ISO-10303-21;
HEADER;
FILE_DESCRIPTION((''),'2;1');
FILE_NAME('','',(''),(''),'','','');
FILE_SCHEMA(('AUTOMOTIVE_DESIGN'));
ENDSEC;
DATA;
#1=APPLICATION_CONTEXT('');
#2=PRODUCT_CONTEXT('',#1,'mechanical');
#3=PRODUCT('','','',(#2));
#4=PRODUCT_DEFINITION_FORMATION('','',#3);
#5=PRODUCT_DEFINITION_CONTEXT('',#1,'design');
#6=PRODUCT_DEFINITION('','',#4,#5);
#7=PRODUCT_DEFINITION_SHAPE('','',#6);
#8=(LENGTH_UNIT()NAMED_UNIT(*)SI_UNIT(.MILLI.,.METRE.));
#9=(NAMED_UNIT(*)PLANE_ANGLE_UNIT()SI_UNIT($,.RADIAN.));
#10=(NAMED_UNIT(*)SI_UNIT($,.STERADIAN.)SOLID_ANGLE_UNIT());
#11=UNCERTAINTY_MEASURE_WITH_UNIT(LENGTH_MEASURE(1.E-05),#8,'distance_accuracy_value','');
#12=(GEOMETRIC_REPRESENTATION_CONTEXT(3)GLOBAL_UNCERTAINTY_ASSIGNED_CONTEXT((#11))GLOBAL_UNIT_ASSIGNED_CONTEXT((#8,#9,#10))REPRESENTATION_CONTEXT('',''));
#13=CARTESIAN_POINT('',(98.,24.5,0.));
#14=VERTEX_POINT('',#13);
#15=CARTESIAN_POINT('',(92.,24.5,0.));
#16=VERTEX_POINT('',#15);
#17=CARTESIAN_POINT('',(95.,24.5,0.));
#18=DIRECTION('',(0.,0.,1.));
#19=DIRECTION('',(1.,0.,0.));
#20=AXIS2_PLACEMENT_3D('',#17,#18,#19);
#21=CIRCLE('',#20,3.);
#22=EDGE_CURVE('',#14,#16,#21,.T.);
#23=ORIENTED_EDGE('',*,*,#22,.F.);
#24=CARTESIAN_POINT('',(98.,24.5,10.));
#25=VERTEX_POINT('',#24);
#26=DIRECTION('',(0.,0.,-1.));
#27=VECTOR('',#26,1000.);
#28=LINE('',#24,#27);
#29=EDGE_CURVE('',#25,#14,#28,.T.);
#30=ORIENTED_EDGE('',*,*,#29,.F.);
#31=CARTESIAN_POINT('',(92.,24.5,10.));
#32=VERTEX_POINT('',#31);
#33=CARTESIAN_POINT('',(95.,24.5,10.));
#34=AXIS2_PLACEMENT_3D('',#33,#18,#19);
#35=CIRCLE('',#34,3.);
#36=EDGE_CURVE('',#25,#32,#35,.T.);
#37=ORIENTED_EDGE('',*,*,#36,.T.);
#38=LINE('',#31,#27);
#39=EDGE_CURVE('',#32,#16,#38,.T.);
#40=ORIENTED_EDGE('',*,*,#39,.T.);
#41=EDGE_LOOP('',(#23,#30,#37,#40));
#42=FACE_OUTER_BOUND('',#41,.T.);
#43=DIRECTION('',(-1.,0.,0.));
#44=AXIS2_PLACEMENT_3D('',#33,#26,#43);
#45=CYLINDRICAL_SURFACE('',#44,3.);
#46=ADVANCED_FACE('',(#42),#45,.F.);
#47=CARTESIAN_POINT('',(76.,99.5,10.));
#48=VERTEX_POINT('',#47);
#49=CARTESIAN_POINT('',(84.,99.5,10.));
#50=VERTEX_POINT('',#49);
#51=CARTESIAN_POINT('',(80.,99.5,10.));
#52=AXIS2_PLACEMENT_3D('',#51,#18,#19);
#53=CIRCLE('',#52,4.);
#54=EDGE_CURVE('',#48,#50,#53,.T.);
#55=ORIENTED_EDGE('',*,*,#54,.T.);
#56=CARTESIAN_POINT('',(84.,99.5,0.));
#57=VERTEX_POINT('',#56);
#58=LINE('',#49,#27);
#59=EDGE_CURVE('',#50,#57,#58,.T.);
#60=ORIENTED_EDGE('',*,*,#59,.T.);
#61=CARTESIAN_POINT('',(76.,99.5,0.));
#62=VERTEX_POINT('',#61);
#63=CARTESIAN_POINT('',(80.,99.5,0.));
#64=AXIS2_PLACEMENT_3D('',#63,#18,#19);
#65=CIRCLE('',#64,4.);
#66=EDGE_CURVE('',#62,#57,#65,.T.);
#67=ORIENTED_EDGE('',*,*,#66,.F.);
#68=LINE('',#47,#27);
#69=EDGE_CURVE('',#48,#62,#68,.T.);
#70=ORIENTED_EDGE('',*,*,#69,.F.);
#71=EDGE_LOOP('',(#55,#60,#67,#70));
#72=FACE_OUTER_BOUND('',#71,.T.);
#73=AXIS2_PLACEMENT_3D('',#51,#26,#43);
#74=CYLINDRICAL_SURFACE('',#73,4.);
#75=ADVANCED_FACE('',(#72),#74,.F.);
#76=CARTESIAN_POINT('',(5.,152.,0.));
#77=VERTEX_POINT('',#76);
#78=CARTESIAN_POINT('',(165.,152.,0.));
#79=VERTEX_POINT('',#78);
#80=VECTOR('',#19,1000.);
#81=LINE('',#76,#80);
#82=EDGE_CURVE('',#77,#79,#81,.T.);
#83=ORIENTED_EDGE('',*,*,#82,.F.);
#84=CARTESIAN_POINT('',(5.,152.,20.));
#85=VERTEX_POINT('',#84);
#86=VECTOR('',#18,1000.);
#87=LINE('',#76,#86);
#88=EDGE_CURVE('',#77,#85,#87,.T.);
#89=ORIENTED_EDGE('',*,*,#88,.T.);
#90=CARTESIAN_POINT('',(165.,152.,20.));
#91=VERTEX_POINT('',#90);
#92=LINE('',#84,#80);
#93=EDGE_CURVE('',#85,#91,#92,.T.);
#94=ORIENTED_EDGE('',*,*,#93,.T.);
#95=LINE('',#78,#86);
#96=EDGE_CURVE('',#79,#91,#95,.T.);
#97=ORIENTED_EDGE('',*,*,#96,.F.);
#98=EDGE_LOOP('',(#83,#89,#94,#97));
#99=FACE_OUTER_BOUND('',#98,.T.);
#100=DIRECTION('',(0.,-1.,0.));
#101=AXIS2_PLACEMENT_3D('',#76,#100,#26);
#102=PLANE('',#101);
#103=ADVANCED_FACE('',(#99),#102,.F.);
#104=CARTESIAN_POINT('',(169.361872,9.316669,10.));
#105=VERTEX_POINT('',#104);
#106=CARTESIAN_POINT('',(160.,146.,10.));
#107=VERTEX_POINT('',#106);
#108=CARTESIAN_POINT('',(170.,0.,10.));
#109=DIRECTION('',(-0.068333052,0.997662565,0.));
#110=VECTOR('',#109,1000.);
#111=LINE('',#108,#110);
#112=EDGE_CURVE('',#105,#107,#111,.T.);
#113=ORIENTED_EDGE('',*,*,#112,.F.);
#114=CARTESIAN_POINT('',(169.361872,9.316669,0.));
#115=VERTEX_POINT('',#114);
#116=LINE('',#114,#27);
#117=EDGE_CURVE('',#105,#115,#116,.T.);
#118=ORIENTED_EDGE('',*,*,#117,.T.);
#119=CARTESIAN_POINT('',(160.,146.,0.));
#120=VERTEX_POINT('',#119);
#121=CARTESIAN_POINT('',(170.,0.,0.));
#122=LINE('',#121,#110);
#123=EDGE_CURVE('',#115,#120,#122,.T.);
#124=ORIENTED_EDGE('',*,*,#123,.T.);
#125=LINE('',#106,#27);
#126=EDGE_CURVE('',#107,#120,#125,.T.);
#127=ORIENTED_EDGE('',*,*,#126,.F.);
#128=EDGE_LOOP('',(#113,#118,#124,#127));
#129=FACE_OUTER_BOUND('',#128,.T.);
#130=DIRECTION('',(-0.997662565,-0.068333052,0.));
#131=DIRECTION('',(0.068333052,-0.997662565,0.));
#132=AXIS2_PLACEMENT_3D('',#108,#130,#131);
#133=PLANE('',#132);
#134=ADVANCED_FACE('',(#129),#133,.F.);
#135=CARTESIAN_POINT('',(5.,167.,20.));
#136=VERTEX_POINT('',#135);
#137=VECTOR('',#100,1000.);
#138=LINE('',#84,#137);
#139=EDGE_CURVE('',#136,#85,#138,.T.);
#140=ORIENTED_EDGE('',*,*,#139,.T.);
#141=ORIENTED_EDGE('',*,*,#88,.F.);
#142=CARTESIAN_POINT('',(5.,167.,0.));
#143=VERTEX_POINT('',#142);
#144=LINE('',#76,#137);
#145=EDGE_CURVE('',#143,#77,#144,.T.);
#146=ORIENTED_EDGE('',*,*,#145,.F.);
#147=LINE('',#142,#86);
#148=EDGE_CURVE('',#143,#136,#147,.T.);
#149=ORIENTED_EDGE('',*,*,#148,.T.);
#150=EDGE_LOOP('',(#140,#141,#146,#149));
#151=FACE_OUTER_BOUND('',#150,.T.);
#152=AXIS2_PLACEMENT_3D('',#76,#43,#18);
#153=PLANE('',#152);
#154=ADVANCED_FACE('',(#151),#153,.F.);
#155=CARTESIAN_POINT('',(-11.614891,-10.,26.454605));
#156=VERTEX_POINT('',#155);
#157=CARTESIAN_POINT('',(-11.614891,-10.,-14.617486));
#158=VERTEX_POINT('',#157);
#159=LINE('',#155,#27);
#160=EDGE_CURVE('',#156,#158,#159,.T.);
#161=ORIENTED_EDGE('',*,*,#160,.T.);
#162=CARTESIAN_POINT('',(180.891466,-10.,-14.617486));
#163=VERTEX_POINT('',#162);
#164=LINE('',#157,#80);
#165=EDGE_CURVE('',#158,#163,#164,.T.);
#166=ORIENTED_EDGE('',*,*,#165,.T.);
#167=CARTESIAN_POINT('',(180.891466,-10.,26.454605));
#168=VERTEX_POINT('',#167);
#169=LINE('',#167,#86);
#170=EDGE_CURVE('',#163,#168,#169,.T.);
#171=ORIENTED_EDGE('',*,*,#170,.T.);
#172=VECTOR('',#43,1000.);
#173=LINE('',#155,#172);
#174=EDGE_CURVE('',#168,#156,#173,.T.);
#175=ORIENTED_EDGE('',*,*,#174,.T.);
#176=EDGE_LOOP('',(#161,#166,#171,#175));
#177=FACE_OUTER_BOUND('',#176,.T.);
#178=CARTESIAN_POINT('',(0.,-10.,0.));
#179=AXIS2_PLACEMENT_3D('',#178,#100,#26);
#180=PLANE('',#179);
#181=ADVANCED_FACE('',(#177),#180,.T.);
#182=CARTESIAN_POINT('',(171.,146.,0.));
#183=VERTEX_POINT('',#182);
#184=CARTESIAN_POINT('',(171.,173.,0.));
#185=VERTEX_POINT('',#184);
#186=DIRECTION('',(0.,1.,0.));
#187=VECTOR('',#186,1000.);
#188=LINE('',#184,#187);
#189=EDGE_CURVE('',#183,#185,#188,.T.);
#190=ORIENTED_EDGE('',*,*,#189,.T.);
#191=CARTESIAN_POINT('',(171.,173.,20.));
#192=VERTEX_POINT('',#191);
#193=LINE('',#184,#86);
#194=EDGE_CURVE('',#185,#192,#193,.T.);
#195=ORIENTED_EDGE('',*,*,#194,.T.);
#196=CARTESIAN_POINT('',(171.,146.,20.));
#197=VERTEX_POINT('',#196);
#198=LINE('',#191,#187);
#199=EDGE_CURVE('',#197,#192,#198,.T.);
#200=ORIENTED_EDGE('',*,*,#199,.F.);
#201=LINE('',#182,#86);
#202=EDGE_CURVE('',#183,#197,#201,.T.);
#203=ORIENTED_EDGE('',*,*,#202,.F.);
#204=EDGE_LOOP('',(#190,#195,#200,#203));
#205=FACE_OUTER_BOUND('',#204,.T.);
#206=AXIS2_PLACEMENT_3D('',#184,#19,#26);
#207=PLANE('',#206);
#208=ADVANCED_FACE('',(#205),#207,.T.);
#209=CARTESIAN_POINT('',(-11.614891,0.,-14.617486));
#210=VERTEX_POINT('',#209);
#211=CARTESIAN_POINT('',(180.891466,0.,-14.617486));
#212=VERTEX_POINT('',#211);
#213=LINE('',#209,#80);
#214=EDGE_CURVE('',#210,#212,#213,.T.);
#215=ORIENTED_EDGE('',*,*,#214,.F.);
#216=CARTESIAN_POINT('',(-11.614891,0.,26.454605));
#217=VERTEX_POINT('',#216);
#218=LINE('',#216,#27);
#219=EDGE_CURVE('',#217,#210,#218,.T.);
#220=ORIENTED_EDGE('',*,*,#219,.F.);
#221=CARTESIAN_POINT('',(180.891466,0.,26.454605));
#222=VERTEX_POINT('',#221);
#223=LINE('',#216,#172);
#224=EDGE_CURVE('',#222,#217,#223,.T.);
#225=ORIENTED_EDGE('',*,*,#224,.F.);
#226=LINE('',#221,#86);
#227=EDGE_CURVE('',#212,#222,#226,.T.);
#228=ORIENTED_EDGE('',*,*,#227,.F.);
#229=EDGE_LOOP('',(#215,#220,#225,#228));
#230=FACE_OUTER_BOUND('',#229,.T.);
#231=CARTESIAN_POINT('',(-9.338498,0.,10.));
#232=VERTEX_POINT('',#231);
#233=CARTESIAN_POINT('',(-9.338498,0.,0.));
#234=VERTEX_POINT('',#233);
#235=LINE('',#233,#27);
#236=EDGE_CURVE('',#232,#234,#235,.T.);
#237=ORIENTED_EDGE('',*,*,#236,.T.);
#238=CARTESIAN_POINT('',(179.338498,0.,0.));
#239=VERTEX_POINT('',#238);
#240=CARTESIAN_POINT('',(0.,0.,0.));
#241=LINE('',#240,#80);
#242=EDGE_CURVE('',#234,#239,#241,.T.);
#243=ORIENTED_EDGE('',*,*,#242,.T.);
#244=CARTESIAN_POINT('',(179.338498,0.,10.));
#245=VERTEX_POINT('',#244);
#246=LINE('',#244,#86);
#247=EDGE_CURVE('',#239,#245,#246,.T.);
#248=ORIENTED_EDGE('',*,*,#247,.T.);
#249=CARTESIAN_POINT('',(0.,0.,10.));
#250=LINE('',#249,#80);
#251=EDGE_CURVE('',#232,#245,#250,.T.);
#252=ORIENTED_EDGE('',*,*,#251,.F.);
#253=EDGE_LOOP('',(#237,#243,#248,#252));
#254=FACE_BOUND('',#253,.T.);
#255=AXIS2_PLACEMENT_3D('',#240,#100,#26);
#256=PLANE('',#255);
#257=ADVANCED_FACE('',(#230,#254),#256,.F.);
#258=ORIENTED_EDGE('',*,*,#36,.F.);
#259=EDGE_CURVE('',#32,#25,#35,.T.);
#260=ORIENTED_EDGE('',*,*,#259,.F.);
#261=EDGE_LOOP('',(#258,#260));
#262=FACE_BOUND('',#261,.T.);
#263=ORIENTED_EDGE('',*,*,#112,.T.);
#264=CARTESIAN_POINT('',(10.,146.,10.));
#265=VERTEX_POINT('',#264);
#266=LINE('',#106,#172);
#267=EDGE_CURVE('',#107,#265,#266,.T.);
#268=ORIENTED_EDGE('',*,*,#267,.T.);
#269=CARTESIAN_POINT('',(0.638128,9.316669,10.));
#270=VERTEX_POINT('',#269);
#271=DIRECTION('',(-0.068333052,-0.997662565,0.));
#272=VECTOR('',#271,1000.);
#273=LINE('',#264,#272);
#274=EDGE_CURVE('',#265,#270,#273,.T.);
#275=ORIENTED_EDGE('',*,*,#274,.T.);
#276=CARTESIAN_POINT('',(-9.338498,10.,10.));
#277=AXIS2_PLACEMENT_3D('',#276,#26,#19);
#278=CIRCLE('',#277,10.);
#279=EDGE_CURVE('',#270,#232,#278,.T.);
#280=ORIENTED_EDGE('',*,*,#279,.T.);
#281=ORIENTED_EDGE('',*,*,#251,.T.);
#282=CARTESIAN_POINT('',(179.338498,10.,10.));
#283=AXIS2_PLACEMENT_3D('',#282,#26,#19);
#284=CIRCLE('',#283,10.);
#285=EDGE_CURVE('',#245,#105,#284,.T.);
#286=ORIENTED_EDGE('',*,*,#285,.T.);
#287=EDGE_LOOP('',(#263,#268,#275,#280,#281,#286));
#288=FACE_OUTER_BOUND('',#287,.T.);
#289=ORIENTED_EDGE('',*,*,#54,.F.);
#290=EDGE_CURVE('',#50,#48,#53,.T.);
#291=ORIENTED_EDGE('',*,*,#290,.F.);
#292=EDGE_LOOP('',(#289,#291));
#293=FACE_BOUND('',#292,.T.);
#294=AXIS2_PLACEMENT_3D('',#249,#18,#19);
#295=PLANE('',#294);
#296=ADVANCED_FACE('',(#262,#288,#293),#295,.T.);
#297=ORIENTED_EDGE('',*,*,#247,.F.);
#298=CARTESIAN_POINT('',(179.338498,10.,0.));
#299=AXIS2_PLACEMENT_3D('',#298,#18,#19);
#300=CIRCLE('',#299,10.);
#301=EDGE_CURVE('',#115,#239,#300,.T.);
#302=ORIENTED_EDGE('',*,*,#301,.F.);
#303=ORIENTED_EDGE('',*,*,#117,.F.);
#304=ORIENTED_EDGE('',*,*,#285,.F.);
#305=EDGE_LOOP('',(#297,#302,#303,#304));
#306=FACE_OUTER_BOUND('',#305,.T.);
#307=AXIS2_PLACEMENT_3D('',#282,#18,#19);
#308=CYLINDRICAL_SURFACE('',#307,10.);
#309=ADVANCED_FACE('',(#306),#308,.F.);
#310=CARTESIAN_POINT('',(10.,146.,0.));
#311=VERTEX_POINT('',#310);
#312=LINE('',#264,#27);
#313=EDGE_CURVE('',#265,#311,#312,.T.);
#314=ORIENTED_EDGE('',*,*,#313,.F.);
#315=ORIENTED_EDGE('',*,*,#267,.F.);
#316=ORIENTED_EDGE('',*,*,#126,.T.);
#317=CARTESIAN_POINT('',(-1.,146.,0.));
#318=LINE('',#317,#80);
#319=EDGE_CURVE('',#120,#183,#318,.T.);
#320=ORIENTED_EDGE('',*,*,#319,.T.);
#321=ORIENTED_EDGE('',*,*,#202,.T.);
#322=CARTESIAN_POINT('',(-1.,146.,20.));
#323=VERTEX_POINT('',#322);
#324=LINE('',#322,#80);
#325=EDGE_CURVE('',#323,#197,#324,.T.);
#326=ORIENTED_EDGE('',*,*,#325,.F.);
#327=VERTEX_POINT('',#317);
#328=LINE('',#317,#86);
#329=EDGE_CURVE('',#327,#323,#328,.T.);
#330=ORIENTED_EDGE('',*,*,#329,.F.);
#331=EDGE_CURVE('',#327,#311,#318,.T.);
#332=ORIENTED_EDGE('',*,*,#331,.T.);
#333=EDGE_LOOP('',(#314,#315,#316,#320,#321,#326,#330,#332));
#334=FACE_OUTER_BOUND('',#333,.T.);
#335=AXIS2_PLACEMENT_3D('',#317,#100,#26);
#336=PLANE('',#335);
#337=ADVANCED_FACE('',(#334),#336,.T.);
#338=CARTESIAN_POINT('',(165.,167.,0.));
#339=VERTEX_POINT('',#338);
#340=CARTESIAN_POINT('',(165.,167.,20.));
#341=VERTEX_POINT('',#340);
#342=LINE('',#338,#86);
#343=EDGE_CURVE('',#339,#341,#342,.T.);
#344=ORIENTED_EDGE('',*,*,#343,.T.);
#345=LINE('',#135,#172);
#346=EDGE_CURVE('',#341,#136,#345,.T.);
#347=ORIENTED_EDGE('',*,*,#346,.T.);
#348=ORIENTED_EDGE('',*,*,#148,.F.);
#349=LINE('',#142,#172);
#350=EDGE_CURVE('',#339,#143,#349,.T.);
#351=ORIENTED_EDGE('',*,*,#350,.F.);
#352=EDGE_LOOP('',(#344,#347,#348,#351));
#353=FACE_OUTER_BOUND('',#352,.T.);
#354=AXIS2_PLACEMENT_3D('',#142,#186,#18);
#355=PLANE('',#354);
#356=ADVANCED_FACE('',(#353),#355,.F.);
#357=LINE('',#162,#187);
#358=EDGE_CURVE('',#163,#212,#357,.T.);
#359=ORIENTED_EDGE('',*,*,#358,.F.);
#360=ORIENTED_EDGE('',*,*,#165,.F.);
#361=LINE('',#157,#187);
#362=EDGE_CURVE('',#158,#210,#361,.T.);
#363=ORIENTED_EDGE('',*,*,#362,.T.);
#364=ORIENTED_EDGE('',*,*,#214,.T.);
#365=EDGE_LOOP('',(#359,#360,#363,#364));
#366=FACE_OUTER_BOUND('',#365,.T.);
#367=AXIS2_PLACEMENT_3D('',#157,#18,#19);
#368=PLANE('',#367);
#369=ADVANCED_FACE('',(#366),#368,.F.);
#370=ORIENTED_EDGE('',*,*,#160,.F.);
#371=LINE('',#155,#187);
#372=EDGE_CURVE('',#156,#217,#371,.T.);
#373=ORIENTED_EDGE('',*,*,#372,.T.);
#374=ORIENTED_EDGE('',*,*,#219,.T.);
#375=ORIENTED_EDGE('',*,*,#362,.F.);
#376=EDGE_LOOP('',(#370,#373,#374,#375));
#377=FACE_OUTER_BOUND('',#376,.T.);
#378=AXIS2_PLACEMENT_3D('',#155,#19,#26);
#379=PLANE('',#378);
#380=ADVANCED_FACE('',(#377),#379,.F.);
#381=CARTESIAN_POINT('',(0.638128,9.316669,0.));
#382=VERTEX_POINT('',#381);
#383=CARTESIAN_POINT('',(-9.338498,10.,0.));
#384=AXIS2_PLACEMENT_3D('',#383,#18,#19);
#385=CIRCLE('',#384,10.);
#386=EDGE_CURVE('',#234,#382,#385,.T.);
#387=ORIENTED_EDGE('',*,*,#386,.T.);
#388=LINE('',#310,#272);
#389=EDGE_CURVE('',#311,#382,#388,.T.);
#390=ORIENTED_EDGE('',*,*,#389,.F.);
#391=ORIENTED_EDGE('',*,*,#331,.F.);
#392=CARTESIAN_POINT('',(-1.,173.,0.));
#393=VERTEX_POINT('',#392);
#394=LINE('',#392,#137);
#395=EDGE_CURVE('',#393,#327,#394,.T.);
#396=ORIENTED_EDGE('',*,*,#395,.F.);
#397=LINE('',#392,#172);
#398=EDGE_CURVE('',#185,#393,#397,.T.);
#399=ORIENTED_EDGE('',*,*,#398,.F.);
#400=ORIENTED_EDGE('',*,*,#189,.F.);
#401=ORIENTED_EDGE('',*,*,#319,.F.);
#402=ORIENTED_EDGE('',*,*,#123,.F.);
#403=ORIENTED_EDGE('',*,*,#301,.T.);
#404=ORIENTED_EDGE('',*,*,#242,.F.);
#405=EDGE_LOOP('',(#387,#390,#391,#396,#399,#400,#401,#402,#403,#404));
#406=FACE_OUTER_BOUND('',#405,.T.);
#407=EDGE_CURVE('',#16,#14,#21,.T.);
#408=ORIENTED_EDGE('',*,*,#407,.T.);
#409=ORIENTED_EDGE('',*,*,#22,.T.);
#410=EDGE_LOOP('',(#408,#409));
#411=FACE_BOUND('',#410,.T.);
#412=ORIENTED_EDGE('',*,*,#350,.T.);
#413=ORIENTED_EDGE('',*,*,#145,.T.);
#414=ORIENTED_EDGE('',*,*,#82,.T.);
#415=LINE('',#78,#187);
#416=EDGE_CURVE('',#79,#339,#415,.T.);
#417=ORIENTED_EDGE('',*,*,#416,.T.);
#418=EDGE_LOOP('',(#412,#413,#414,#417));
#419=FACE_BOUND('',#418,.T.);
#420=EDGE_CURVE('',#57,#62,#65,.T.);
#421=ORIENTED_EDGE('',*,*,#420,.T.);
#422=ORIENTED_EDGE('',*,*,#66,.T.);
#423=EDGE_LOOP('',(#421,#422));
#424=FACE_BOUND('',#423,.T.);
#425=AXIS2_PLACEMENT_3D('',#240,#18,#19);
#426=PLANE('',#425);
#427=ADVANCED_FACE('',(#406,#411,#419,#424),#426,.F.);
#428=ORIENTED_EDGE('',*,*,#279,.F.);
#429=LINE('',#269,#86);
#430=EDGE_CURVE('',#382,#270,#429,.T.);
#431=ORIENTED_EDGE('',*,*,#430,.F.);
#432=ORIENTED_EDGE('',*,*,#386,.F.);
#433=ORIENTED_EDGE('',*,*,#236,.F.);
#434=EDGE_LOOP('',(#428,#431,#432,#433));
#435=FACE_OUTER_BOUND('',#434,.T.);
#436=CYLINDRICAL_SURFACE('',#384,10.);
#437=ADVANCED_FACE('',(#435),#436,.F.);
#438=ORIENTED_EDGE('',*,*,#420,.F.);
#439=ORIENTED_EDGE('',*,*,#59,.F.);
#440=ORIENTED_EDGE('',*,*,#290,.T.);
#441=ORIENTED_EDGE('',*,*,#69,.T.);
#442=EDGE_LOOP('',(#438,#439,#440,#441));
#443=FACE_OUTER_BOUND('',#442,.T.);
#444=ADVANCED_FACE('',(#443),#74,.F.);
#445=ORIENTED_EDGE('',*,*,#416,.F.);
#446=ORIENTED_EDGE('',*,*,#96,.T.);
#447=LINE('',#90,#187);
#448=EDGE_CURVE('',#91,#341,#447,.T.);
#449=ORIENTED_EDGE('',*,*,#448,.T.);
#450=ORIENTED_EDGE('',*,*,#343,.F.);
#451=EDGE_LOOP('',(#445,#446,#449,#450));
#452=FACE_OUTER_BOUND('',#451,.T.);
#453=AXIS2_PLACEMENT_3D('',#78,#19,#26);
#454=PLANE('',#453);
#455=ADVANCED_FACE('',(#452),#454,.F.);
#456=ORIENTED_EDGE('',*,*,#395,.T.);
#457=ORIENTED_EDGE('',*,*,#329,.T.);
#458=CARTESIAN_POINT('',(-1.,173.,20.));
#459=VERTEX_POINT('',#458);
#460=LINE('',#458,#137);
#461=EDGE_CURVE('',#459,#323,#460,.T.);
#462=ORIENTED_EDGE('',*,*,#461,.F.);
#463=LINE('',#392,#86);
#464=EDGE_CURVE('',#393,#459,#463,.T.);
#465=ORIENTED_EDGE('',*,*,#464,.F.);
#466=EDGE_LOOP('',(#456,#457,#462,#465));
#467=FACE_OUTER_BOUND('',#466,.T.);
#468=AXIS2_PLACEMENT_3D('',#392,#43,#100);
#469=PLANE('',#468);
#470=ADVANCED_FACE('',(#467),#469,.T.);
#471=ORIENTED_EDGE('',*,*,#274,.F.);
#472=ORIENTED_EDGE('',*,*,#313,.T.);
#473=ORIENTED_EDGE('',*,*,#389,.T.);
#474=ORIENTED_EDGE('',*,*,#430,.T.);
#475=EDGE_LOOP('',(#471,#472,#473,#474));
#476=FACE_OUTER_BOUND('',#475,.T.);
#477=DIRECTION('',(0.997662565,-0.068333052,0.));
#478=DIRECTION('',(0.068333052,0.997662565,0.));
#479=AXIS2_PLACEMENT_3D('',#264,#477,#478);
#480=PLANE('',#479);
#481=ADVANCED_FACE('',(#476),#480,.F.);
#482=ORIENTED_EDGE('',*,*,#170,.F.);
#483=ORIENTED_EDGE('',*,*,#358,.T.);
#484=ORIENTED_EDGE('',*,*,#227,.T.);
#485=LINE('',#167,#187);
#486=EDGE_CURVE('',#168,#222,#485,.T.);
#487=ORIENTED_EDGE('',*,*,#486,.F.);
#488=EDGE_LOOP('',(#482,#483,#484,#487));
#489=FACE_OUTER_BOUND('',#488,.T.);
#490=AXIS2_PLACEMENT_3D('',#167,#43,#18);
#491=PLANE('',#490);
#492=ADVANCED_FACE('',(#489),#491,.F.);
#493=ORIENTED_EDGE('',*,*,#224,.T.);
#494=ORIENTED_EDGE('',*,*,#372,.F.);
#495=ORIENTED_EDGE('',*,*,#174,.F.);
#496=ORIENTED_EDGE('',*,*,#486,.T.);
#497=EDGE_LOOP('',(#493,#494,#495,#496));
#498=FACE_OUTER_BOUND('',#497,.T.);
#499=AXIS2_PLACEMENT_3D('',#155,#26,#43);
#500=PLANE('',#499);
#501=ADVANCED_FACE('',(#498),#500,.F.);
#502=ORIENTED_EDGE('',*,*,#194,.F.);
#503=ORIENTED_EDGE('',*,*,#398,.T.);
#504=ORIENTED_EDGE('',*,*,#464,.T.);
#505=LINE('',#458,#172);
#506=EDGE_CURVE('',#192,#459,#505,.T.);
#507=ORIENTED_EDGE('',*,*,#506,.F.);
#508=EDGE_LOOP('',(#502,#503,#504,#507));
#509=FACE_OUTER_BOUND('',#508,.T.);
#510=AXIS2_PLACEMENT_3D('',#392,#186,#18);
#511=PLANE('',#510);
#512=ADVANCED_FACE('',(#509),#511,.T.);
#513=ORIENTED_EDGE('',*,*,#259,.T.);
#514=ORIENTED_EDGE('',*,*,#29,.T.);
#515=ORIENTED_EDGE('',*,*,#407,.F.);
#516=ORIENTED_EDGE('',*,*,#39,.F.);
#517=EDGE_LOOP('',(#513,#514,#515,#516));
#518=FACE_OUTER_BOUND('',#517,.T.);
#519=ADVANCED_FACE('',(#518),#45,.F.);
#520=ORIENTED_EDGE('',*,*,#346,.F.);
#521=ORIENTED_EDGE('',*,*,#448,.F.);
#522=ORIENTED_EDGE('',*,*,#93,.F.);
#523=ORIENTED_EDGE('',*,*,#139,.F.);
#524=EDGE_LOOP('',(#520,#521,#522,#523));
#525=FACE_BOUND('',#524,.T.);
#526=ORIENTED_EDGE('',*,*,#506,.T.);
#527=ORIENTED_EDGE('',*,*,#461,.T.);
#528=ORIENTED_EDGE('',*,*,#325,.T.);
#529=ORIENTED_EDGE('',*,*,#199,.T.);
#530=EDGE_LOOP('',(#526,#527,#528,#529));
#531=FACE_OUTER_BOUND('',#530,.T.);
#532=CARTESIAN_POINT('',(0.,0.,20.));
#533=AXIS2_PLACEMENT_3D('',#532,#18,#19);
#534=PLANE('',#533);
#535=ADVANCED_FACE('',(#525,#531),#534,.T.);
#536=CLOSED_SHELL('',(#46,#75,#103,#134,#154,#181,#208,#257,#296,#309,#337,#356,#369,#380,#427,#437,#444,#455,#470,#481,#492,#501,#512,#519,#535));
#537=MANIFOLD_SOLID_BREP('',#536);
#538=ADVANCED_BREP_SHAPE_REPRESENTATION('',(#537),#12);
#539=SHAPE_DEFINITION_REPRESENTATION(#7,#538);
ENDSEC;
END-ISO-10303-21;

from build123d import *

# Parameters (mm, degrees)
SKETCH1_R           = 3
SKETCH1_R_2         = 4
BOSS_EXTRUDE1_DEPTH = 10
SKETCH2_W           = 192.506357526
SKETCH2_H           = 41.072090777
BOSS_EXTRUDE2_DEPTH = 10
FILLET1_R           = 10
SKETCH3_W           = 172
SKETCH3_H           = 27
SKETCH3_W_2         = 160
SKETCH3_H_2         = 15
BOSS_EXTRUDE3_DEPTH = 10


with BuildPart() as part:
    # Sketch1 → Boss-Extrude1 (new body)
    with BuildSketch(Plane.XY):
        Polygon((0, 0), (170, 0), (160, 146), (10, 146), align=None)
        with Locations((95, 24.5)):
            Circle(SKETCH1_R, mode=Mode.SUBTRACT)
        with Locations((80, 99.5)):
            Circle(SKETCH1_R_2, mode=Mode.SUBTRACT)
    extrude(amount=BOSS_EXTRUDE1_DEPTH)

    # Sketch2 → Boss-Extrude2 (add)
    with BuildSketch(Plane(origin=(0, 0, 0), x_dir=(-1, 0, 0), z_dir=(0, -1, 0))):
        with Locations((-84.638287431, -5.918559418)):
            Rectangle(SKETCH2_W, SKETCH2_H)
    extrude(amount=BOSS_EXTRUDE2_DEPTH)

    # Fillet1
    fillet1_edges = [part.edges().sort_by_distance(p)[0] for p in [
        (170, 0, 5),
        (0, 0, 5),
    ]]
    fillet(fillet1_edges, radius=FILLET1_R)

    # Sketch3 → Boss-Extrude3 (add, symmetric)
    with BuildSketch(Plane.XY.offset(10)):
        with Locations((85, 159.5)):
            Rectangle(SKETCH3_W, SKETCH3_H)
        with Locations((85, 159.5)):
            Rectangle(SKETCH3_W_2, SKETCH3_H_2, mode=Mode.SUBTRACT)
    extrude(amount=BOSS_EXTRUDE3_DEPTH, both=True)


solid = part.part
